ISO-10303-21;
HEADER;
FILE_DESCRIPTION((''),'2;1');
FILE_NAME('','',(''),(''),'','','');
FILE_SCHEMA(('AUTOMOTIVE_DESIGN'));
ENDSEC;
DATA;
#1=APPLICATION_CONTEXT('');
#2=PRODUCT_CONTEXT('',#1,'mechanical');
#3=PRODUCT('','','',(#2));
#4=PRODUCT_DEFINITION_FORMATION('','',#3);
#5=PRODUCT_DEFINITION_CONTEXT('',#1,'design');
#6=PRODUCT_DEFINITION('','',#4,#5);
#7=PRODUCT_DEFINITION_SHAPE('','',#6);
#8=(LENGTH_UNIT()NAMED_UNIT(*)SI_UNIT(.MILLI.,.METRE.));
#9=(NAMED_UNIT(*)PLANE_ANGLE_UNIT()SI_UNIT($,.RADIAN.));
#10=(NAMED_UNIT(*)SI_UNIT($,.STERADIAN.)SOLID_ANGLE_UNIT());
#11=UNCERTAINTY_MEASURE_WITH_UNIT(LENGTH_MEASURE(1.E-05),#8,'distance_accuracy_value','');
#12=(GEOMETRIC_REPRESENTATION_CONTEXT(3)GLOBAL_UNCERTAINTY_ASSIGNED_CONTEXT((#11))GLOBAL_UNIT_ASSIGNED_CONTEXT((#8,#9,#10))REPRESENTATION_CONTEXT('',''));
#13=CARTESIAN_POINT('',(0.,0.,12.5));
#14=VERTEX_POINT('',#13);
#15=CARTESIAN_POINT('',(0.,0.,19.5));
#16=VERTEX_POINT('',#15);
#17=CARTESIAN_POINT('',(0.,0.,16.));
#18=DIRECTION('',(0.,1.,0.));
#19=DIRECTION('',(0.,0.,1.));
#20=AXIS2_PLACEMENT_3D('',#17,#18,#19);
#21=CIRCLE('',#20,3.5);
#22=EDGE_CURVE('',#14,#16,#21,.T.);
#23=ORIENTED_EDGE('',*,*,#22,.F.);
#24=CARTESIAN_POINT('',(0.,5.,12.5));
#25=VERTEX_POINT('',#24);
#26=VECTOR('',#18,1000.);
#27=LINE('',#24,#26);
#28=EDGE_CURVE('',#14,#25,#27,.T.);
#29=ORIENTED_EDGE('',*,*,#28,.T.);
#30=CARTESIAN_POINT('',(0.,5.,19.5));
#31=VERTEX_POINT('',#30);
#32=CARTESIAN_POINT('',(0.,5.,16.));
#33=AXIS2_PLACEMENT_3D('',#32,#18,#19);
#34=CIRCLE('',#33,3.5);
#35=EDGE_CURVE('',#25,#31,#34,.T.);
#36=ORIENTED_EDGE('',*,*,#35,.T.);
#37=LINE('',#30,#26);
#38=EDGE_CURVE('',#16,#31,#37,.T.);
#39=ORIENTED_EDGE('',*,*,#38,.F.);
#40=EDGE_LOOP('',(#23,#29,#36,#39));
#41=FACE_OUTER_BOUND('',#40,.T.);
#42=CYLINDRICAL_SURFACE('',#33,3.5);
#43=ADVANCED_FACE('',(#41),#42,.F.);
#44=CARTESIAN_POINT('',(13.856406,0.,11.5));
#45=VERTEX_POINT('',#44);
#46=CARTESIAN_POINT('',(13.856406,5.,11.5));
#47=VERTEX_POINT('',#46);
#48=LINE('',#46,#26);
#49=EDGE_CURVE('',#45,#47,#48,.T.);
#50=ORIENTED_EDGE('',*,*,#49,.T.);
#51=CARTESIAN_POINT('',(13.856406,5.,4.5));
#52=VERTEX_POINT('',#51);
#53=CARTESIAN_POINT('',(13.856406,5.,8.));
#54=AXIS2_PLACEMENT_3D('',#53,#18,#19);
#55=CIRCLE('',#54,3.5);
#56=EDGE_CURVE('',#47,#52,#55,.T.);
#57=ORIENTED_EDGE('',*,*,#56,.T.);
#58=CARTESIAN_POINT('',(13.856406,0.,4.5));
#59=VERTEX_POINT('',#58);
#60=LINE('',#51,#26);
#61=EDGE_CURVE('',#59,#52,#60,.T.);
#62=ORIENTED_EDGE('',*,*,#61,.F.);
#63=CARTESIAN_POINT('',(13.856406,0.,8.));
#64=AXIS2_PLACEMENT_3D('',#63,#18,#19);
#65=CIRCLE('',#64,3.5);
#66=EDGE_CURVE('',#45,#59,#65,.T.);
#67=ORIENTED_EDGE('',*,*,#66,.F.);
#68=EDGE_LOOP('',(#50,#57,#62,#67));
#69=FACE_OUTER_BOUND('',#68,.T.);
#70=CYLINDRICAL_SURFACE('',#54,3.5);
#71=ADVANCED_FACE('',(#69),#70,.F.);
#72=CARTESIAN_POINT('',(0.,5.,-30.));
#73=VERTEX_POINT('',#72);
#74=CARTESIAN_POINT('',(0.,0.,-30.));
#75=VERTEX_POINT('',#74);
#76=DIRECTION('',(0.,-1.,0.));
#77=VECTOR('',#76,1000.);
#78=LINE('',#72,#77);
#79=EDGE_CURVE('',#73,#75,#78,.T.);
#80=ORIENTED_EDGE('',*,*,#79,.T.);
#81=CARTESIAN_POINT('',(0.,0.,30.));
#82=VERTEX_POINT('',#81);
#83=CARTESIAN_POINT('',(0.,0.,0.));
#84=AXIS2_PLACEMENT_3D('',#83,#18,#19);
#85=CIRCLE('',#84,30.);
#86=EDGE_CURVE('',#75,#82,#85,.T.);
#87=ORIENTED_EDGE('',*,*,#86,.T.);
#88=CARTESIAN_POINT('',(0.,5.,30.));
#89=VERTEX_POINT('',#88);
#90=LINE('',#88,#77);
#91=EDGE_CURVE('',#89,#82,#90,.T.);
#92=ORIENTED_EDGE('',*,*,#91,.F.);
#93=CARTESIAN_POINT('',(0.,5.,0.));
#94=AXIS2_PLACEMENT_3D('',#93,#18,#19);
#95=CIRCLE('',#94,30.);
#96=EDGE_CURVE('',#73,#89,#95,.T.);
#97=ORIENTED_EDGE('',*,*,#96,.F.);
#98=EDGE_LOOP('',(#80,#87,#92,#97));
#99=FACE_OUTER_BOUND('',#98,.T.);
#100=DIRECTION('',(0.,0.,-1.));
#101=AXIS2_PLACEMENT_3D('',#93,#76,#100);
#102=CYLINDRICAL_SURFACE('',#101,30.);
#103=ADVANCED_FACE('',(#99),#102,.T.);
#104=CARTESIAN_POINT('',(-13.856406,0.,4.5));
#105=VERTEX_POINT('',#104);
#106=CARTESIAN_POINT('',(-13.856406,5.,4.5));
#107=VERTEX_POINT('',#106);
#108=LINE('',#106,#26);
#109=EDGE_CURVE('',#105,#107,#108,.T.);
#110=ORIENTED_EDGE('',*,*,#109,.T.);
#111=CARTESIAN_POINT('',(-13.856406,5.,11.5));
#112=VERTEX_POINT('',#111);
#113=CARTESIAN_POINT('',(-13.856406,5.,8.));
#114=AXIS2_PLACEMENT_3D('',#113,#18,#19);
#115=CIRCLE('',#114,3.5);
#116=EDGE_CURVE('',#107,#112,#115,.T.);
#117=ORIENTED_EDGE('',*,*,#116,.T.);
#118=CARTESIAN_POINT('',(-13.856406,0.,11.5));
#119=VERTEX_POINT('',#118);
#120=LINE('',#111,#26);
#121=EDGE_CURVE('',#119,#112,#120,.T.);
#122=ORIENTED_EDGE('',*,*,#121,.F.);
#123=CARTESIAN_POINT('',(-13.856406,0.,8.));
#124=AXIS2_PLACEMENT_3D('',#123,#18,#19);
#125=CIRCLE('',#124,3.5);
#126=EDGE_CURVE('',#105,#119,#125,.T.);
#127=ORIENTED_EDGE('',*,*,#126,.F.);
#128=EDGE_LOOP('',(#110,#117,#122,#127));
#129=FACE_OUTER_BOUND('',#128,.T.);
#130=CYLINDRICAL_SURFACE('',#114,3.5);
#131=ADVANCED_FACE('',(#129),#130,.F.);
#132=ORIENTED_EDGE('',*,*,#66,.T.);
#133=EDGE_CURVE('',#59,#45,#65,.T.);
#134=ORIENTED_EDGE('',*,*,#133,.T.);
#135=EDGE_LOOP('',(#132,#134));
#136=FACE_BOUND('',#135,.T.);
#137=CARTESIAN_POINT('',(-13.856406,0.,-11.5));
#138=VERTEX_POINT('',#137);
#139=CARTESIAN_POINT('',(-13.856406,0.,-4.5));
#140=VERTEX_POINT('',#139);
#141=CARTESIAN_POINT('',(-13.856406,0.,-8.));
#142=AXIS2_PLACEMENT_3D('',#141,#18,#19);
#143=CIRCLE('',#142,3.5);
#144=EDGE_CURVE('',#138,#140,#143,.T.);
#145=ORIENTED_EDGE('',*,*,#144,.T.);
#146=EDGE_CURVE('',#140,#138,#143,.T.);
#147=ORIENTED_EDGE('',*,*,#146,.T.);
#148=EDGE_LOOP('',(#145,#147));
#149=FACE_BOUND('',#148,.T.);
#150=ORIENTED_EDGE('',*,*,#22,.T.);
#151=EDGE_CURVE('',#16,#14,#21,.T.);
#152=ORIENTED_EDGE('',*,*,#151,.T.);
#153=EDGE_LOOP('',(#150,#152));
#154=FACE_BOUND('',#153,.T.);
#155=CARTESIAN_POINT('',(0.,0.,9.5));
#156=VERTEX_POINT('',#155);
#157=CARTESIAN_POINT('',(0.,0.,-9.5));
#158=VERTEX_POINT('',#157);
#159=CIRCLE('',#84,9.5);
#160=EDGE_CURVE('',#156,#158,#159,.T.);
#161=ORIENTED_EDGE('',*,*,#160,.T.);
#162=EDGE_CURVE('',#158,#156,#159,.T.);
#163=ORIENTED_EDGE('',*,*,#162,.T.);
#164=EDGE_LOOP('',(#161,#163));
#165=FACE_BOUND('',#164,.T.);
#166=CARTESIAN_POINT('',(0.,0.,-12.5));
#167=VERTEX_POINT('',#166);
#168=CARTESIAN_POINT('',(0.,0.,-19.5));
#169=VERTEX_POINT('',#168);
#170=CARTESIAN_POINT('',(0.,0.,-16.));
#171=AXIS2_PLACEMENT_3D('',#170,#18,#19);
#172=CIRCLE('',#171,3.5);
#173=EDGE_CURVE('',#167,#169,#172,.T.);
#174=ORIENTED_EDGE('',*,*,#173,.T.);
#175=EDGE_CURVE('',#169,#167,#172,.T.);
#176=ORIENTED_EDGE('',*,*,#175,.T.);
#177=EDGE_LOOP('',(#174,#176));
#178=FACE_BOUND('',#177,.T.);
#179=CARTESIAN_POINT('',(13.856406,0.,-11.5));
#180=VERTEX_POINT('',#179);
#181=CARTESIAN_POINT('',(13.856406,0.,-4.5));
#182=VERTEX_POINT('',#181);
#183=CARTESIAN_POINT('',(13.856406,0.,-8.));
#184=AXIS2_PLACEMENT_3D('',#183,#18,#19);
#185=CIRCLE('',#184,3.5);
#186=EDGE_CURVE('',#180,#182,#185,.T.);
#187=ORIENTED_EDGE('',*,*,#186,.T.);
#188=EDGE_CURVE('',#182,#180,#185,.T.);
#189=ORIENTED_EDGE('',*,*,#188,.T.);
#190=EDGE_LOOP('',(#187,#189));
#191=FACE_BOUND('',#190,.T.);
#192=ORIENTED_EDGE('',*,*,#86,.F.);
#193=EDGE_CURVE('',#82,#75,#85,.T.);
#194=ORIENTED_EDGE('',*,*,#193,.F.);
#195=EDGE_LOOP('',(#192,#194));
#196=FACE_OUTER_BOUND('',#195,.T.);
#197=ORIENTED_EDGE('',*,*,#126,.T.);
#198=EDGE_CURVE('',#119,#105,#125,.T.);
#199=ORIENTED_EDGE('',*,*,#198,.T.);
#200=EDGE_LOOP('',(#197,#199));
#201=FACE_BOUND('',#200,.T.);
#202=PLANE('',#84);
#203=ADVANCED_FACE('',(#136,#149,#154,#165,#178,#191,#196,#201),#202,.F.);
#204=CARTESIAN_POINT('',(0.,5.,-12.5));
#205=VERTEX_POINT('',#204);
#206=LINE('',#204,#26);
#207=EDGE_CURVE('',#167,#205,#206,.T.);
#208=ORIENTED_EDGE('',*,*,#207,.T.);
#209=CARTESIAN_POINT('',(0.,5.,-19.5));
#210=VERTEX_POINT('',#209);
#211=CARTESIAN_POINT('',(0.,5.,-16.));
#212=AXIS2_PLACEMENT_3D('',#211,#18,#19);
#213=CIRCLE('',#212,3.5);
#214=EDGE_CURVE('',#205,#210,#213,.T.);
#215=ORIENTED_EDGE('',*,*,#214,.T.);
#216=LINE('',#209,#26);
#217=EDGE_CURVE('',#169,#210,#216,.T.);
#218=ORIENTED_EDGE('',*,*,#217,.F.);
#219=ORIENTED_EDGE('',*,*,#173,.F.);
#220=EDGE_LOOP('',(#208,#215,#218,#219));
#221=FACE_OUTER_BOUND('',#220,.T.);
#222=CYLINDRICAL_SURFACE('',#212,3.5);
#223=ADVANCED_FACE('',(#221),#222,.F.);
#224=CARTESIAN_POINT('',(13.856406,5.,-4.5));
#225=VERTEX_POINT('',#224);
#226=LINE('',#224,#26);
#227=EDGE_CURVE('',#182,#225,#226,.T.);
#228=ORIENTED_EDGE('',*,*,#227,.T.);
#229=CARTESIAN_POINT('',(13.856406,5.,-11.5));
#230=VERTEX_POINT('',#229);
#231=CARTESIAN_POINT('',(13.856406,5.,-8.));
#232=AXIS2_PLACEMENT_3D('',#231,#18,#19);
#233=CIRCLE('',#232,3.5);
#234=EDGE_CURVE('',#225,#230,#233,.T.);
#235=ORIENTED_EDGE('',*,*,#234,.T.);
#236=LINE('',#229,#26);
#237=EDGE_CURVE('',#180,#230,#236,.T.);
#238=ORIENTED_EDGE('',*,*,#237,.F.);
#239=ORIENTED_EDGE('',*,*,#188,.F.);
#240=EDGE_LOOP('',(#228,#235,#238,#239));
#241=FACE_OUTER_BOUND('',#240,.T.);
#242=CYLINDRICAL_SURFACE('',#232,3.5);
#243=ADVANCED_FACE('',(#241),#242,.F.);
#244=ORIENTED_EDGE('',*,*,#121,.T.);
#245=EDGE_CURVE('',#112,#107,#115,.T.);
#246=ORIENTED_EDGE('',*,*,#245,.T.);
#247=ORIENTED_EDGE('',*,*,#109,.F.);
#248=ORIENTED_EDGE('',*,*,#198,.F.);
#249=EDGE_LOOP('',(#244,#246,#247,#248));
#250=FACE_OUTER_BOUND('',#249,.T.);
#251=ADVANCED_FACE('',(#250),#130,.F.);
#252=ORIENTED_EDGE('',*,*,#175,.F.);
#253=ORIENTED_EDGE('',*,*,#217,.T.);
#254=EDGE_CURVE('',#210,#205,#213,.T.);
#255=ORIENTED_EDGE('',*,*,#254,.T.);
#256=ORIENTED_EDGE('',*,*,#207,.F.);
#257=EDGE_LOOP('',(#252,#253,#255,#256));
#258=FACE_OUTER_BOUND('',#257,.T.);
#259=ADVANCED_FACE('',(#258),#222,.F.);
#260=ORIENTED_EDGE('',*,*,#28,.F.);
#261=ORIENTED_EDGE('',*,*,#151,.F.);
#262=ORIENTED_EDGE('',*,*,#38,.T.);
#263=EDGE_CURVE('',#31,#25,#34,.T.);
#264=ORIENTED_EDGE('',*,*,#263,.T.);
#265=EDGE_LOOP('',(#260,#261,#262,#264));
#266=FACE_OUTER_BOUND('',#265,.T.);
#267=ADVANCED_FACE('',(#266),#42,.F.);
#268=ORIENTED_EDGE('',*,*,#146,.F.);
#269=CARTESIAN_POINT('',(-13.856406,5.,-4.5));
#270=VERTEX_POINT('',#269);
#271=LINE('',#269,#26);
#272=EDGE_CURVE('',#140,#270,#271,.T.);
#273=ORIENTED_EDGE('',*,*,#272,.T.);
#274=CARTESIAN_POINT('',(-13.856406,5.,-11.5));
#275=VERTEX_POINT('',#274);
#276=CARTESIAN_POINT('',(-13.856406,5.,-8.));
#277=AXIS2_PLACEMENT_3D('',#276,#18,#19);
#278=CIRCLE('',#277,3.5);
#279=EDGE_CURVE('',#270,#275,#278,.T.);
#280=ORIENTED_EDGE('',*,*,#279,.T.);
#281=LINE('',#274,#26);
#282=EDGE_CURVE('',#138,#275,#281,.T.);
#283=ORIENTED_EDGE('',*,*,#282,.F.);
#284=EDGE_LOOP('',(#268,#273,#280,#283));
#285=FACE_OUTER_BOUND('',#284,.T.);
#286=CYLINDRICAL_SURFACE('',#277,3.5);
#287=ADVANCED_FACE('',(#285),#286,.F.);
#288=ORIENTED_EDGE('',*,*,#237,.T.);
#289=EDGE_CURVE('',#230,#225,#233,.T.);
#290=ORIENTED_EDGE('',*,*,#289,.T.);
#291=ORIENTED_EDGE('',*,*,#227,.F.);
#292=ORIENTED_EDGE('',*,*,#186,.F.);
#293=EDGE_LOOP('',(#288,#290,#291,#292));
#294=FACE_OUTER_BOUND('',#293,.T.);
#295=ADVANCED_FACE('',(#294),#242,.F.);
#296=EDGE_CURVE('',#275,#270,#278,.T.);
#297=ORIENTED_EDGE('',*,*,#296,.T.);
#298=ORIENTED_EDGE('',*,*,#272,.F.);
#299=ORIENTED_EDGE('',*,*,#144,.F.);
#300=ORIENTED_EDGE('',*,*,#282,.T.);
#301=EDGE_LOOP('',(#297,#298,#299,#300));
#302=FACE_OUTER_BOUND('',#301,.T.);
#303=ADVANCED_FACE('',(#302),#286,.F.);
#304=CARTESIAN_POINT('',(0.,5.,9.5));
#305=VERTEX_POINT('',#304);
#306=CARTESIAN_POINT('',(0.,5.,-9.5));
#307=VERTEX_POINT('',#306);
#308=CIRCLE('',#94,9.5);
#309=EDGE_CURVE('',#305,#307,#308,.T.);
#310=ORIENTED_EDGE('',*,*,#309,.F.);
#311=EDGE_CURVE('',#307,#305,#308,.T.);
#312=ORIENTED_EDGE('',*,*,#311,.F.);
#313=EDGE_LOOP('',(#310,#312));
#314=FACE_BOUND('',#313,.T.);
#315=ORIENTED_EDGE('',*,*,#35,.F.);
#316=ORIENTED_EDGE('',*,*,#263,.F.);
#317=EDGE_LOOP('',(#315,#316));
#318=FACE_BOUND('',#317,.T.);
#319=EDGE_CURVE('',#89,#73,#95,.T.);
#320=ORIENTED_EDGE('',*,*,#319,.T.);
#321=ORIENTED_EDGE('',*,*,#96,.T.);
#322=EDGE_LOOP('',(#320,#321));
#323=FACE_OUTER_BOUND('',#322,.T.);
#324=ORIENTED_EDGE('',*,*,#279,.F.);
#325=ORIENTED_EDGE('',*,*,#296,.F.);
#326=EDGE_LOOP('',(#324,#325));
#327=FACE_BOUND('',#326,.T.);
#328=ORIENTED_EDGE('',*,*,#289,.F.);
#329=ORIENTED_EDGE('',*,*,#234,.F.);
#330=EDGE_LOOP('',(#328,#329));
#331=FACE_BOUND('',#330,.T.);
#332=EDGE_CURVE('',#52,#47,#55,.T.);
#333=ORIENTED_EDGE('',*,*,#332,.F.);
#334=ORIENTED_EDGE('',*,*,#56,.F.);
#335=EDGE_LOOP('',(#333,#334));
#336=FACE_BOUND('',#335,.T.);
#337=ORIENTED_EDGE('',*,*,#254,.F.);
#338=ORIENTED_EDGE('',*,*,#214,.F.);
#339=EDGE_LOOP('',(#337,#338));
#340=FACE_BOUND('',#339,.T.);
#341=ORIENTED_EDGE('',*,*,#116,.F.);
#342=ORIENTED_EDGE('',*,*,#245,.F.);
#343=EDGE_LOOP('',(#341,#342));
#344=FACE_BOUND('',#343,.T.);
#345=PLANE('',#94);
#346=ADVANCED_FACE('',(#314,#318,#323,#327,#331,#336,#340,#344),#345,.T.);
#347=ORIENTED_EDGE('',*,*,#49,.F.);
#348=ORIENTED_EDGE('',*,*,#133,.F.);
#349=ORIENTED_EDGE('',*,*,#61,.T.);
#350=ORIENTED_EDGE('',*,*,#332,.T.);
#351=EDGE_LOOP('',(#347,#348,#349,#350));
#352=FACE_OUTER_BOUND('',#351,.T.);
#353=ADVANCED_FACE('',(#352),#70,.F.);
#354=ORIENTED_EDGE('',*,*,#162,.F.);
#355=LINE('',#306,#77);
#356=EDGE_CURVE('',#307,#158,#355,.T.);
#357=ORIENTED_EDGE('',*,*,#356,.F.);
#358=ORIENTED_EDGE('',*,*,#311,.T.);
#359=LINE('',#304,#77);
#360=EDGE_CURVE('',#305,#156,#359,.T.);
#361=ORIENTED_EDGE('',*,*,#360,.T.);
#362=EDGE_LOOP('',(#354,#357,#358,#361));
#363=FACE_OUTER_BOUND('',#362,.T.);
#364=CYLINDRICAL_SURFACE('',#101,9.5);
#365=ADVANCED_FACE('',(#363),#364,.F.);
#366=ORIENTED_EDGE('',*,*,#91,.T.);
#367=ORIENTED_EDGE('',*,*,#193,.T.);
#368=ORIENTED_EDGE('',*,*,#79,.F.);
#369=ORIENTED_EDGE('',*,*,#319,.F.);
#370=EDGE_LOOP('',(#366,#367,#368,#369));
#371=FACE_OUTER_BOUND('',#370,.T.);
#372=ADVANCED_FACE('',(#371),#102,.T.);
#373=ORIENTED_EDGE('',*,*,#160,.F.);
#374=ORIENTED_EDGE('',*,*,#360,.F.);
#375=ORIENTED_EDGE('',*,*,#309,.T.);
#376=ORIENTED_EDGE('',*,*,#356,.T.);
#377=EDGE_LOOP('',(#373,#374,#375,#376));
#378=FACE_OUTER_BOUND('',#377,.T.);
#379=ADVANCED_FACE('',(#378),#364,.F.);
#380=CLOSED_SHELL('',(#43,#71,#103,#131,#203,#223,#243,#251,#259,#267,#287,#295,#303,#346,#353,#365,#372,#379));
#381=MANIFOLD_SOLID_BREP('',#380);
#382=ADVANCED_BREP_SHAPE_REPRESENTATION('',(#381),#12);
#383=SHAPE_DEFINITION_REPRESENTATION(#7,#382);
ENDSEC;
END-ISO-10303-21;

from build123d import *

# Parameters (mm, degrees)
SKETCH_1_R         = 30
SKETCH_1_R_2       = 9.5
EXTRUDE_1_DEPTH    = 5
HOLE_WIZARD_M6_1_D = 7


with BuildPart() as part:
    # 草图1 → 凸台-拉伸1 (new body)
    with BuildSketch(Plane(origin=(0, 0, 0), x_dir=(1, 0, 0), z_dir=(0, 1, 0))):
        with Locations(Location((0, 0, 0), (0, 0, 270))):
            Circle(SKETCH_1_R)
        with Locations(Location((0, 0, 0), (0, 0, 270))):
            Circle(SKETCH_1_R_2, mode=Mode.SUBTRACT)
    extrude(amount=EXTRUDE_1_DEPTH)

    # M6 间隙孔1 (through all)
    with Locations(Plane(origin=(0, 5, 0), x_dir=(1, 0, 0), z_dir=(0, 1, 0))):
        with Locations((0, 16), (13.856406461, 8), (13.856406461, -8), (0, -16), (-13.856406461, -8), (-13.856406461, 8)):
            Hole(HOLE_WIZARD_M6_1_D / 2)


solid = part.part
